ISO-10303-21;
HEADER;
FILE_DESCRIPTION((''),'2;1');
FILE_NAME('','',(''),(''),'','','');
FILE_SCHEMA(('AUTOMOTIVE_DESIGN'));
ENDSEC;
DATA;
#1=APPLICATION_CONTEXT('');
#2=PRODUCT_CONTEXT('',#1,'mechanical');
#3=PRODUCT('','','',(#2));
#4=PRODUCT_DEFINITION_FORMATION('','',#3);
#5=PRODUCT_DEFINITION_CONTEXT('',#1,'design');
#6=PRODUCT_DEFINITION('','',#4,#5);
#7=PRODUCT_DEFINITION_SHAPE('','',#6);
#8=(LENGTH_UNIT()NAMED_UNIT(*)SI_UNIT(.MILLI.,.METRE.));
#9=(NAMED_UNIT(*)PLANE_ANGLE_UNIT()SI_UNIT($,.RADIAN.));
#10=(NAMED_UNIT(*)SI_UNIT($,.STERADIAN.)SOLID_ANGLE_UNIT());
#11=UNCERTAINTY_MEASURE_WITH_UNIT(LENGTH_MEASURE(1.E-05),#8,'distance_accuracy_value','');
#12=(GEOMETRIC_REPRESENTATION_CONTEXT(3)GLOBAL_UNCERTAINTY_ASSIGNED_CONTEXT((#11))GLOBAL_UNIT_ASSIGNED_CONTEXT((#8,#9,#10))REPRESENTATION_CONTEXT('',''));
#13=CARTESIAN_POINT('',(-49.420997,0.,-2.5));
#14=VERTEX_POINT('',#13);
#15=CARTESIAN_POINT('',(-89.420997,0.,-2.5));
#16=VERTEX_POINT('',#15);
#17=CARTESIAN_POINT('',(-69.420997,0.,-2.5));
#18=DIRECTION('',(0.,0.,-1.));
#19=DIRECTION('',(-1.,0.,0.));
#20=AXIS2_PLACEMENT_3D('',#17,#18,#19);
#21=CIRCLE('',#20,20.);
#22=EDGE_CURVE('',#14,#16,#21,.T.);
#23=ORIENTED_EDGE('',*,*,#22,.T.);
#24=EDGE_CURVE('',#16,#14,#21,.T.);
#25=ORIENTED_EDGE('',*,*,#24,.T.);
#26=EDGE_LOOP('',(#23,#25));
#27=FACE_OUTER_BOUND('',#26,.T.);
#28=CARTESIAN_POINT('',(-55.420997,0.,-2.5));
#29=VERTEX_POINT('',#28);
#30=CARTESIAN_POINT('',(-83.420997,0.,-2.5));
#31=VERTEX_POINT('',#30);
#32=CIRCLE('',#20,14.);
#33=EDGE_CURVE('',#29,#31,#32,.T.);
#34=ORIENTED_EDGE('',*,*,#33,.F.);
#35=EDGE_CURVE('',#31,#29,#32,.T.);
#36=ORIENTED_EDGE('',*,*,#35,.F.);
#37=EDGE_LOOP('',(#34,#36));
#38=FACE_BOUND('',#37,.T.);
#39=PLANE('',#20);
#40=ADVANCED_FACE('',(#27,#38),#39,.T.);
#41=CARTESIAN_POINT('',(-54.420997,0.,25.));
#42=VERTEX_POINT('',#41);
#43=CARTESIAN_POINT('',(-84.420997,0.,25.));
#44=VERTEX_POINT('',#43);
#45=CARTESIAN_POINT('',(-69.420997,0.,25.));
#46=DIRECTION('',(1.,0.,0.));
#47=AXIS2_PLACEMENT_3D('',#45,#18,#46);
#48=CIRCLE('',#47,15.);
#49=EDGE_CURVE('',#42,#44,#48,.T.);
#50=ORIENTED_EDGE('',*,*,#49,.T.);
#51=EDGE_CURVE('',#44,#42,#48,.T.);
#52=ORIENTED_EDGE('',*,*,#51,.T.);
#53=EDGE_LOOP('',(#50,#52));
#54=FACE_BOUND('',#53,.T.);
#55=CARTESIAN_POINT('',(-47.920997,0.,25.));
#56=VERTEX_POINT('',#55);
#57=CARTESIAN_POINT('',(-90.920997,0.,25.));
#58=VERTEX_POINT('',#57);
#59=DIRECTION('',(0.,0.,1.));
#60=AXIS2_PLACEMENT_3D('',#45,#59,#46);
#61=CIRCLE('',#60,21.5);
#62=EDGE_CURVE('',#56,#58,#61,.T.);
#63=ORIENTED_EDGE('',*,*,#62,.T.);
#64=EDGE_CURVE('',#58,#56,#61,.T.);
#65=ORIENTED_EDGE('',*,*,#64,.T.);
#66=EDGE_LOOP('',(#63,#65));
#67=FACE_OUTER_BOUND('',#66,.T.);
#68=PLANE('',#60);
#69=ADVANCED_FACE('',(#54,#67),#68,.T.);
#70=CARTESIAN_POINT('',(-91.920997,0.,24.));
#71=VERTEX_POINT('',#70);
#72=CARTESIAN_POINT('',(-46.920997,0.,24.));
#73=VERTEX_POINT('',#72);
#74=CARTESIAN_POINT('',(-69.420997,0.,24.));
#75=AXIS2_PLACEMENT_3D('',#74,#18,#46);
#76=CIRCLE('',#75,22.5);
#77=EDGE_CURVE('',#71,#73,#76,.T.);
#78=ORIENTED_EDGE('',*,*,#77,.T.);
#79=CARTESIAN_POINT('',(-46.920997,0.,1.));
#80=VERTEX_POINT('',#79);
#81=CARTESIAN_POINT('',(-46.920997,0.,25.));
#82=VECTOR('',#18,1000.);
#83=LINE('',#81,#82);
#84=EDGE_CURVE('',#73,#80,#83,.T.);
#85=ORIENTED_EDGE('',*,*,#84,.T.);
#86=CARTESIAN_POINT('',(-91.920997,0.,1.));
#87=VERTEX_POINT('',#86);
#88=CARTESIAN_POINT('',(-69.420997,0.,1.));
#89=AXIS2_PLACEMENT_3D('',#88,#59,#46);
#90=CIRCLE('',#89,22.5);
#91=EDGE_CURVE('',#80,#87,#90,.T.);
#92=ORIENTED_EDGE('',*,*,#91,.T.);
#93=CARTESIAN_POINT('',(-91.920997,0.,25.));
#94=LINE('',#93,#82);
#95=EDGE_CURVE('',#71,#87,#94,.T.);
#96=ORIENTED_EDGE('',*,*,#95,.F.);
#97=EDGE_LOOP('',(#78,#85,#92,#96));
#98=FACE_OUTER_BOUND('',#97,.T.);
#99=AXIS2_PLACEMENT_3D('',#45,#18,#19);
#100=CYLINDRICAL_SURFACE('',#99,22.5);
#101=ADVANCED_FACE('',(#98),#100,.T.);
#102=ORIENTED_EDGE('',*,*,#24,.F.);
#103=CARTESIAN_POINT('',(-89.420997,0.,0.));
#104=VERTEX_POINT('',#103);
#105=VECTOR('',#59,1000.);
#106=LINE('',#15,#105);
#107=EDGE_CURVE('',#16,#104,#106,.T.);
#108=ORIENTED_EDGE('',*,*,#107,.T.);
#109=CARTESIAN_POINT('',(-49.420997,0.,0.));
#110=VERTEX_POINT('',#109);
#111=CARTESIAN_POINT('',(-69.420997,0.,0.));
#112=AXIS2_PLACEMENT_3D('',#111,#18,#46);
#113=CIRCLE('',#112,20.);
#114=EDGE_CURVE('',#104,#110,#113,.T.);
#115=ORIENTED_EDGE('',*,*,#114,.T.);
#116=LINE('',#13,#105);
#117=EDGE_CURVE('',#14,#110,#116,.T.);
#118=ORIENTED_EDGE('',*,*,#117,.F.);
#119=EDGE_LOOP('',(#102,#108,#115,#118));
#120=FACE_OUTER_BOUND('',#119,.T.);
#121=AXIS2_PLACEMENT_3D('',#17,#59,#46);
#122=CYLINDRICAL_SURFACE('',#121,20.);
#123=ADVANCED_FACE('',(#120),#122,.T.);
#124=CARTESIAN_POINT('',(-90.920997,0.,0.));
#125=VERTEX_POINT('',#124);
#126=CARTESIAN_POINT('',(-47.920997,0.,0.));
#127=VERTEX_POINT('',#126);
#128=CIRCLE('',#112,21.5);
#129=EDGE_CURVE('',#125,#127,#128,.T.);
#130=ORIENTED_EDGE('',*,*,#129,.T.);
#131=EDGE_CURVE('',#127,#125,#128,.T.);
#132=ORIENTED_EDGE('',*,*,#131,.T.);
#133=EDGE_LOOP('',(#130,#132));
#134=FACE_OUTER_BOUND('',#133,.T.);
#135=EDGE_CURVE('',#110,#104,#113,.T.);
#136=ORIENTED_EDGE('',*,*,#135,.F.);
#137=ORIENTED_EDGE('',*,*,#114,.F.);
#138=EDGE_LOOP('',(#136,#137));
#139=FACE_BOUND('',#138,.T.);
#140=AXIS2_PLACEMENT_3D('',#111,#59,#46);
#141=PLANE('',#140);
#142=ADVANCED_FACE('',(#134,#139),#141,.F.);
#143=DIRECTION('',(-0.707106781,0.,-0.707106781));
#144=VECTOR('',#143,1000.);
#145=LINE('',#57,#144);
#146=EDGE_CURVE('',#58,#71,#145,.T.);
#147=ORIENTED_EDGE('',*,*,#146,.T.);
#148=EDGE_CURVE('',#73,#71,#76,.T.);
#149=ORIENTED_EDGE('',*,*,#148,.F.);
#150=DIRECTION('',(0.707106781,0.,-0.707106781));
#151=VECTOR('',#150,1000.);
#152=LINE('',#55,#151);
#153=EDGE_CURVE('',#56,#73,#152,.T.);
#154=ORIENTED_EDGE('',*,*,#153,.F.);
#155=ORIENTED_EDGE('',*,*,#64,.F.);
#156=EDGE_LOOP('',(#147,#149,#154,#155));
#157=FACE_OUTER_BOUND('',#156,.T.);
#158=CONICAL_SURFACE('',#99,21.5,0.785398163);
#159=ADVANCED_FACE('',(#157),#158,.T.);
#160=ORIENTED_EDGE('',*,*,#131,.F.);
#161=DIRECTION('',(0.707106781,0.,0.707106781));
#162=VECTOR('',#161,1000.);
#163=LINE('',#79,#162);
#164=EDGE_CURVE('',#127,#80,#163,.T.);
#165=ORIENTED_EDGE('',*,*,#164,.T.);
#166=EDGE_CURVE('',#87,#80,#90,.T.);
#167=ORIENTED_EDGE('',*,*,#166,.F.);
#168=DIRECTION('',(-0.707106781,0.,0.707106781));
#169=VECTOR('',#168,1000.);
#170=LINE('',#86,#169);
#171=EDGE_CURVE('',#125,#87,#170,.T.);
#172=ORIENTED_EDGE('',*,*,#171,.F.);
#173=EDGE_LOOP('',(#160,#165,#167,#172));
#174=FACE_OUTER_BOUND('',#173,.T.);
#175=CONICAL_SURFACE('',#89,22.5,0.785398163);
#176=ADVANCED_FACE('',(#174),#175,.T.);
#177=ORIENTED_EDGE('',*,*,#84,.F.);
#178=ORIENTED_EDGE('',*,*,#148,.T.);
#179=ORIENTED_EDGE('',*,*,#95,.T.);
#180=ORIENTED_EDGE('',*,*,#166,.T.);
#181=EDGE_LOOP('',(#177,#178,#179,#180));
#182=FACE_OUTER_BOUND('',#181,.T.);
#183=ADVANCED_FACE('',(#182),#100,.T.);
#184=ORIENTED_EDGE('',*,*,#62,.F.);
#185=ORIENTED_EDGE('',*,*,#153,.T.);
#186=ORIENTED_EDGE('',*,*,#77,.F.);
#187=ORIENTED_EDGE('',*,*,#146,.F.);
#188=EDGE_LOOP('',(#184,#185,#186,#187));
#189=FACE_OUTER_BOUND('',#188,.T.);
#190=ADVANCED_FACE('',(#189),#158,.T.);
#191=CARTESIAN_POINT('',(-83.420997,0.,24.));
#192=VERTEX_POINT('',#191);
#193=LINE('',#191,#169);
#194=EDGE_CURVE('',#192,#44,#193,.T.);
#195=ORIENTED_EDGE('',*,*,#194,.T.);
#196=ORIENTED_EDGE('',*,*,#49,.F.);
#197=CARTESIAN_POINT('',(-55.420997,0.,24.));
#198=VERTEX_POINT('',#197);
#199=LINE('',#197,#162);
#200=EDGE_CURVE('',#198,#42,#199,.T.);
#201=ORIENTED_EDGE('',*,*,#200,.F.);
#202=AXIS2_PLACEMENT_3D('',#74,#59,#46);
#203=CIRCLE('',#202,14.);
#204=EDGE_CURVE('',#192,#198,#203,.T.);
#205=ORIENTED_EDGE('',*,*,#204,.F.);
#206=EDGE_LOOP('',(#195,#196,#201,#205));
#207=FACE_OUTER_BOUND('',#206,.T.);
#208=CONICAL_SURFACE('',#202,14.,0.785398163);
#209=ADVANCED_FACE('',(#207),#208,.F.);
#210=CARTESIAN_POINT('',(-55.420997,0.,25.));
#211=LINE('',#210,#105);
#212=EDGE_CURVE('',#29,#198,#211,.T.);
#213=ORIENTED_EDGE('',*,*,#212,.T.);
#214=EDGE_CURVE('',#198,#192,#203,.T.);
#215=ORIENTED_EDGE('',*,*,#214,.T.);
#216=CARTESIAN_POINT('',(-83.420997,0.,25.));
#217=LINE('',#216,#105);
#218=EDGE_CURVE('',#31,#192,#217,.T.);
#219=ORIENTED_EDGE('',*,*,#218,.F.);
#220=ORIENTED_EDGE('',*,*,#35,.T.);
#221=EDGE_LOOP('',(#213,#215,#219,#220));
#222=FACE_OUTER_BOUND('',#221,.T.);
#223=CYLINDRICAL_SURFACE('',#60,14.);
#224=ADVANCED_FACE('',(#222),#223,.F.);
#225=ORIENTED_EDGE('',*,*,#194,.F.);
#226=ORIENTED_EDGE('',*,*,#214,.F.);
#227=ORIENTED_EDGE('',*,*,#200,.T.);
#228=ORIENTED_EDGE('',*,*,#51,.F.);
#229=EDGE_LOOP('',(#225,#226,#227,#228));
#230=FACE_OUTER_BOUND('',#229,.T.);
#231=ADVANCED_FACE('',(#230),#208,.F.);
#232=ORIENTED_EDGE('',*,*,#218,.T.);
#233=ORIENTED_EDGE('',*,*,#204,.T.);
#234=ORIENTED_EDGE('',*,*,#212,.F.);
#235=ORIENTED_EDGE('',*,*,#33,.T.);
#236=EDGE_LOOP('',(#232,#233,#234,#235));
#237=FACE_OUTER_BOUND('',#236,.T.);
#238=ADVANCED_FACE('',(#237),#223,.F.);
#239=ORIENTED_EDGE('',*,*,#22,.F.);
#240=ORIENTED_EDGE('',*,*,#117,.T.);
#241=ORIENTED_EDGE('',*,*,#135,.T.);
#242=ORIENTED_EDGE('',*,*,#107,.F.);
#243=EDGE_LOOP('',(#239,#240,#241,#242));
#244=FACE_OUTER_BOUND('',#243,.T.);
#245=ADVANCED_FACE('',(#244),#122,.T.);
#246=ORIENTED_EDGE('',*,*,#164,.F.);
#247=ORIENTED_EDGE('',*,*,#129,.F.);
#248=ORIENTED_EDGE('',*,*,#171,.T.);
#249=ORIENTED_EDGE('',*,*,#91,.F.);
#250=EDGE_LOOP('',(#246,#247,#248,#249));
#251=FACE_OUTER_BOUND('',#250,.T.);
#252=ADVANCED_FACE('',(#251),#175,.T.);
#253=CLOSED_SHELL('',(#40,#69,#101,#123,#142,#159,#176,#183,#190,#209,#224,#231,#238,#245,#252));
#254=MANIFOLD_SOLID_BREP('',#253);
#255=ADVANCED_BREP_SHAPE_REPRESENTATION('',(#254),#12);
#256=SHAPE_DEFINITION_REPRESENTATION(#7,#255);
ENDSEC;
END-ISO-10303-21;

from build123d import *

# Parameters (mm, degrees)
SKETCH8_R                  = 22.5
BOSS_EXTRUDE2_DEPTH        = 25
M30X2_0_TAPPED_HOLE1_D     = 28
M30X2_0_TAPPED_HOLE1_DEPTH = 70
M30X2_0_TAPPED_HOLE1_TIP   = 8.412048666
BOSS_EXTRUDE3_START        = 2.5
SKETCH11_R                 = 20
SKETCH11_R_2               = 14
BOSS_EXTRUDE3_DEPTH        = 2.5
CHAMFER1_SIZE              = 1


with BuildPart() as part:
    # Sketch8 → Boss-Extrude2 (new body)
    with BuildSketch(Plane.XY):
        with Locations((-69.420997024, 0)):
            Circle(SKETCH8_R)
    extrude(amount=BOSS_EXTRUDE2_DEPTH)

    # M30x2.0 Tapped Hole1
    with Locations(Plane(origin=(-69.420997024, 0, 25), x_dir=(1, 0, 0), z_dir=(0, 0, 1))):
        with Locations((0, 0)):
            Hole(M30X2_0_TAPPED_HOLE1_D / 2, depth=M30X2_0_TAPPED_HOLE1_DEPTH)
            with Locations((0, 0, -(M30X2_0_TAPPED_HOLE1_DEPTH + M30X2_0_TAPPED_HOLE1_TIP / 2))):  # 118° drill point
                Cone(0, M30X2_0_TAPPED_HOLE1_D / 2, M30X2_0_TAPPED_HOLE1_TIP, mode=Mode.SUBTRACT)

    # Sketch11 → Boss-Extrude3 (add)
    with BuildSketch(Plane(origin=(0, 0, 0), x_dir=(-1, 0, 0), z_dir=(0, 0, -1)).offset(BOSS_EXTRUDE3_START)):
        with Locations(Location((69.420997024, 0, 0), (0, 0, 180))):
            Circle(SKETCH11_R)
        with Locations(Location((69.420997024, 0, 0), (0, 0, 180))):
            Circle(SKETCH11_R_2, mode=Mode.SUBTRACT)
    extrude(amount=-BOSS_EXTRUDE3_DEPTH)

    # Chamfer1
    chamfer1_edges = [part.edges().sort_by_distance(p)[0] for p in [
        (-91.920997024, 0, 0),
        (-91.920997024, 0, 25),
        (-55.420997024, 0, 25),
    ]]
    chamfer(chamfer1_edges, length=CHAMFER1_SIZE)


solid = part.part
